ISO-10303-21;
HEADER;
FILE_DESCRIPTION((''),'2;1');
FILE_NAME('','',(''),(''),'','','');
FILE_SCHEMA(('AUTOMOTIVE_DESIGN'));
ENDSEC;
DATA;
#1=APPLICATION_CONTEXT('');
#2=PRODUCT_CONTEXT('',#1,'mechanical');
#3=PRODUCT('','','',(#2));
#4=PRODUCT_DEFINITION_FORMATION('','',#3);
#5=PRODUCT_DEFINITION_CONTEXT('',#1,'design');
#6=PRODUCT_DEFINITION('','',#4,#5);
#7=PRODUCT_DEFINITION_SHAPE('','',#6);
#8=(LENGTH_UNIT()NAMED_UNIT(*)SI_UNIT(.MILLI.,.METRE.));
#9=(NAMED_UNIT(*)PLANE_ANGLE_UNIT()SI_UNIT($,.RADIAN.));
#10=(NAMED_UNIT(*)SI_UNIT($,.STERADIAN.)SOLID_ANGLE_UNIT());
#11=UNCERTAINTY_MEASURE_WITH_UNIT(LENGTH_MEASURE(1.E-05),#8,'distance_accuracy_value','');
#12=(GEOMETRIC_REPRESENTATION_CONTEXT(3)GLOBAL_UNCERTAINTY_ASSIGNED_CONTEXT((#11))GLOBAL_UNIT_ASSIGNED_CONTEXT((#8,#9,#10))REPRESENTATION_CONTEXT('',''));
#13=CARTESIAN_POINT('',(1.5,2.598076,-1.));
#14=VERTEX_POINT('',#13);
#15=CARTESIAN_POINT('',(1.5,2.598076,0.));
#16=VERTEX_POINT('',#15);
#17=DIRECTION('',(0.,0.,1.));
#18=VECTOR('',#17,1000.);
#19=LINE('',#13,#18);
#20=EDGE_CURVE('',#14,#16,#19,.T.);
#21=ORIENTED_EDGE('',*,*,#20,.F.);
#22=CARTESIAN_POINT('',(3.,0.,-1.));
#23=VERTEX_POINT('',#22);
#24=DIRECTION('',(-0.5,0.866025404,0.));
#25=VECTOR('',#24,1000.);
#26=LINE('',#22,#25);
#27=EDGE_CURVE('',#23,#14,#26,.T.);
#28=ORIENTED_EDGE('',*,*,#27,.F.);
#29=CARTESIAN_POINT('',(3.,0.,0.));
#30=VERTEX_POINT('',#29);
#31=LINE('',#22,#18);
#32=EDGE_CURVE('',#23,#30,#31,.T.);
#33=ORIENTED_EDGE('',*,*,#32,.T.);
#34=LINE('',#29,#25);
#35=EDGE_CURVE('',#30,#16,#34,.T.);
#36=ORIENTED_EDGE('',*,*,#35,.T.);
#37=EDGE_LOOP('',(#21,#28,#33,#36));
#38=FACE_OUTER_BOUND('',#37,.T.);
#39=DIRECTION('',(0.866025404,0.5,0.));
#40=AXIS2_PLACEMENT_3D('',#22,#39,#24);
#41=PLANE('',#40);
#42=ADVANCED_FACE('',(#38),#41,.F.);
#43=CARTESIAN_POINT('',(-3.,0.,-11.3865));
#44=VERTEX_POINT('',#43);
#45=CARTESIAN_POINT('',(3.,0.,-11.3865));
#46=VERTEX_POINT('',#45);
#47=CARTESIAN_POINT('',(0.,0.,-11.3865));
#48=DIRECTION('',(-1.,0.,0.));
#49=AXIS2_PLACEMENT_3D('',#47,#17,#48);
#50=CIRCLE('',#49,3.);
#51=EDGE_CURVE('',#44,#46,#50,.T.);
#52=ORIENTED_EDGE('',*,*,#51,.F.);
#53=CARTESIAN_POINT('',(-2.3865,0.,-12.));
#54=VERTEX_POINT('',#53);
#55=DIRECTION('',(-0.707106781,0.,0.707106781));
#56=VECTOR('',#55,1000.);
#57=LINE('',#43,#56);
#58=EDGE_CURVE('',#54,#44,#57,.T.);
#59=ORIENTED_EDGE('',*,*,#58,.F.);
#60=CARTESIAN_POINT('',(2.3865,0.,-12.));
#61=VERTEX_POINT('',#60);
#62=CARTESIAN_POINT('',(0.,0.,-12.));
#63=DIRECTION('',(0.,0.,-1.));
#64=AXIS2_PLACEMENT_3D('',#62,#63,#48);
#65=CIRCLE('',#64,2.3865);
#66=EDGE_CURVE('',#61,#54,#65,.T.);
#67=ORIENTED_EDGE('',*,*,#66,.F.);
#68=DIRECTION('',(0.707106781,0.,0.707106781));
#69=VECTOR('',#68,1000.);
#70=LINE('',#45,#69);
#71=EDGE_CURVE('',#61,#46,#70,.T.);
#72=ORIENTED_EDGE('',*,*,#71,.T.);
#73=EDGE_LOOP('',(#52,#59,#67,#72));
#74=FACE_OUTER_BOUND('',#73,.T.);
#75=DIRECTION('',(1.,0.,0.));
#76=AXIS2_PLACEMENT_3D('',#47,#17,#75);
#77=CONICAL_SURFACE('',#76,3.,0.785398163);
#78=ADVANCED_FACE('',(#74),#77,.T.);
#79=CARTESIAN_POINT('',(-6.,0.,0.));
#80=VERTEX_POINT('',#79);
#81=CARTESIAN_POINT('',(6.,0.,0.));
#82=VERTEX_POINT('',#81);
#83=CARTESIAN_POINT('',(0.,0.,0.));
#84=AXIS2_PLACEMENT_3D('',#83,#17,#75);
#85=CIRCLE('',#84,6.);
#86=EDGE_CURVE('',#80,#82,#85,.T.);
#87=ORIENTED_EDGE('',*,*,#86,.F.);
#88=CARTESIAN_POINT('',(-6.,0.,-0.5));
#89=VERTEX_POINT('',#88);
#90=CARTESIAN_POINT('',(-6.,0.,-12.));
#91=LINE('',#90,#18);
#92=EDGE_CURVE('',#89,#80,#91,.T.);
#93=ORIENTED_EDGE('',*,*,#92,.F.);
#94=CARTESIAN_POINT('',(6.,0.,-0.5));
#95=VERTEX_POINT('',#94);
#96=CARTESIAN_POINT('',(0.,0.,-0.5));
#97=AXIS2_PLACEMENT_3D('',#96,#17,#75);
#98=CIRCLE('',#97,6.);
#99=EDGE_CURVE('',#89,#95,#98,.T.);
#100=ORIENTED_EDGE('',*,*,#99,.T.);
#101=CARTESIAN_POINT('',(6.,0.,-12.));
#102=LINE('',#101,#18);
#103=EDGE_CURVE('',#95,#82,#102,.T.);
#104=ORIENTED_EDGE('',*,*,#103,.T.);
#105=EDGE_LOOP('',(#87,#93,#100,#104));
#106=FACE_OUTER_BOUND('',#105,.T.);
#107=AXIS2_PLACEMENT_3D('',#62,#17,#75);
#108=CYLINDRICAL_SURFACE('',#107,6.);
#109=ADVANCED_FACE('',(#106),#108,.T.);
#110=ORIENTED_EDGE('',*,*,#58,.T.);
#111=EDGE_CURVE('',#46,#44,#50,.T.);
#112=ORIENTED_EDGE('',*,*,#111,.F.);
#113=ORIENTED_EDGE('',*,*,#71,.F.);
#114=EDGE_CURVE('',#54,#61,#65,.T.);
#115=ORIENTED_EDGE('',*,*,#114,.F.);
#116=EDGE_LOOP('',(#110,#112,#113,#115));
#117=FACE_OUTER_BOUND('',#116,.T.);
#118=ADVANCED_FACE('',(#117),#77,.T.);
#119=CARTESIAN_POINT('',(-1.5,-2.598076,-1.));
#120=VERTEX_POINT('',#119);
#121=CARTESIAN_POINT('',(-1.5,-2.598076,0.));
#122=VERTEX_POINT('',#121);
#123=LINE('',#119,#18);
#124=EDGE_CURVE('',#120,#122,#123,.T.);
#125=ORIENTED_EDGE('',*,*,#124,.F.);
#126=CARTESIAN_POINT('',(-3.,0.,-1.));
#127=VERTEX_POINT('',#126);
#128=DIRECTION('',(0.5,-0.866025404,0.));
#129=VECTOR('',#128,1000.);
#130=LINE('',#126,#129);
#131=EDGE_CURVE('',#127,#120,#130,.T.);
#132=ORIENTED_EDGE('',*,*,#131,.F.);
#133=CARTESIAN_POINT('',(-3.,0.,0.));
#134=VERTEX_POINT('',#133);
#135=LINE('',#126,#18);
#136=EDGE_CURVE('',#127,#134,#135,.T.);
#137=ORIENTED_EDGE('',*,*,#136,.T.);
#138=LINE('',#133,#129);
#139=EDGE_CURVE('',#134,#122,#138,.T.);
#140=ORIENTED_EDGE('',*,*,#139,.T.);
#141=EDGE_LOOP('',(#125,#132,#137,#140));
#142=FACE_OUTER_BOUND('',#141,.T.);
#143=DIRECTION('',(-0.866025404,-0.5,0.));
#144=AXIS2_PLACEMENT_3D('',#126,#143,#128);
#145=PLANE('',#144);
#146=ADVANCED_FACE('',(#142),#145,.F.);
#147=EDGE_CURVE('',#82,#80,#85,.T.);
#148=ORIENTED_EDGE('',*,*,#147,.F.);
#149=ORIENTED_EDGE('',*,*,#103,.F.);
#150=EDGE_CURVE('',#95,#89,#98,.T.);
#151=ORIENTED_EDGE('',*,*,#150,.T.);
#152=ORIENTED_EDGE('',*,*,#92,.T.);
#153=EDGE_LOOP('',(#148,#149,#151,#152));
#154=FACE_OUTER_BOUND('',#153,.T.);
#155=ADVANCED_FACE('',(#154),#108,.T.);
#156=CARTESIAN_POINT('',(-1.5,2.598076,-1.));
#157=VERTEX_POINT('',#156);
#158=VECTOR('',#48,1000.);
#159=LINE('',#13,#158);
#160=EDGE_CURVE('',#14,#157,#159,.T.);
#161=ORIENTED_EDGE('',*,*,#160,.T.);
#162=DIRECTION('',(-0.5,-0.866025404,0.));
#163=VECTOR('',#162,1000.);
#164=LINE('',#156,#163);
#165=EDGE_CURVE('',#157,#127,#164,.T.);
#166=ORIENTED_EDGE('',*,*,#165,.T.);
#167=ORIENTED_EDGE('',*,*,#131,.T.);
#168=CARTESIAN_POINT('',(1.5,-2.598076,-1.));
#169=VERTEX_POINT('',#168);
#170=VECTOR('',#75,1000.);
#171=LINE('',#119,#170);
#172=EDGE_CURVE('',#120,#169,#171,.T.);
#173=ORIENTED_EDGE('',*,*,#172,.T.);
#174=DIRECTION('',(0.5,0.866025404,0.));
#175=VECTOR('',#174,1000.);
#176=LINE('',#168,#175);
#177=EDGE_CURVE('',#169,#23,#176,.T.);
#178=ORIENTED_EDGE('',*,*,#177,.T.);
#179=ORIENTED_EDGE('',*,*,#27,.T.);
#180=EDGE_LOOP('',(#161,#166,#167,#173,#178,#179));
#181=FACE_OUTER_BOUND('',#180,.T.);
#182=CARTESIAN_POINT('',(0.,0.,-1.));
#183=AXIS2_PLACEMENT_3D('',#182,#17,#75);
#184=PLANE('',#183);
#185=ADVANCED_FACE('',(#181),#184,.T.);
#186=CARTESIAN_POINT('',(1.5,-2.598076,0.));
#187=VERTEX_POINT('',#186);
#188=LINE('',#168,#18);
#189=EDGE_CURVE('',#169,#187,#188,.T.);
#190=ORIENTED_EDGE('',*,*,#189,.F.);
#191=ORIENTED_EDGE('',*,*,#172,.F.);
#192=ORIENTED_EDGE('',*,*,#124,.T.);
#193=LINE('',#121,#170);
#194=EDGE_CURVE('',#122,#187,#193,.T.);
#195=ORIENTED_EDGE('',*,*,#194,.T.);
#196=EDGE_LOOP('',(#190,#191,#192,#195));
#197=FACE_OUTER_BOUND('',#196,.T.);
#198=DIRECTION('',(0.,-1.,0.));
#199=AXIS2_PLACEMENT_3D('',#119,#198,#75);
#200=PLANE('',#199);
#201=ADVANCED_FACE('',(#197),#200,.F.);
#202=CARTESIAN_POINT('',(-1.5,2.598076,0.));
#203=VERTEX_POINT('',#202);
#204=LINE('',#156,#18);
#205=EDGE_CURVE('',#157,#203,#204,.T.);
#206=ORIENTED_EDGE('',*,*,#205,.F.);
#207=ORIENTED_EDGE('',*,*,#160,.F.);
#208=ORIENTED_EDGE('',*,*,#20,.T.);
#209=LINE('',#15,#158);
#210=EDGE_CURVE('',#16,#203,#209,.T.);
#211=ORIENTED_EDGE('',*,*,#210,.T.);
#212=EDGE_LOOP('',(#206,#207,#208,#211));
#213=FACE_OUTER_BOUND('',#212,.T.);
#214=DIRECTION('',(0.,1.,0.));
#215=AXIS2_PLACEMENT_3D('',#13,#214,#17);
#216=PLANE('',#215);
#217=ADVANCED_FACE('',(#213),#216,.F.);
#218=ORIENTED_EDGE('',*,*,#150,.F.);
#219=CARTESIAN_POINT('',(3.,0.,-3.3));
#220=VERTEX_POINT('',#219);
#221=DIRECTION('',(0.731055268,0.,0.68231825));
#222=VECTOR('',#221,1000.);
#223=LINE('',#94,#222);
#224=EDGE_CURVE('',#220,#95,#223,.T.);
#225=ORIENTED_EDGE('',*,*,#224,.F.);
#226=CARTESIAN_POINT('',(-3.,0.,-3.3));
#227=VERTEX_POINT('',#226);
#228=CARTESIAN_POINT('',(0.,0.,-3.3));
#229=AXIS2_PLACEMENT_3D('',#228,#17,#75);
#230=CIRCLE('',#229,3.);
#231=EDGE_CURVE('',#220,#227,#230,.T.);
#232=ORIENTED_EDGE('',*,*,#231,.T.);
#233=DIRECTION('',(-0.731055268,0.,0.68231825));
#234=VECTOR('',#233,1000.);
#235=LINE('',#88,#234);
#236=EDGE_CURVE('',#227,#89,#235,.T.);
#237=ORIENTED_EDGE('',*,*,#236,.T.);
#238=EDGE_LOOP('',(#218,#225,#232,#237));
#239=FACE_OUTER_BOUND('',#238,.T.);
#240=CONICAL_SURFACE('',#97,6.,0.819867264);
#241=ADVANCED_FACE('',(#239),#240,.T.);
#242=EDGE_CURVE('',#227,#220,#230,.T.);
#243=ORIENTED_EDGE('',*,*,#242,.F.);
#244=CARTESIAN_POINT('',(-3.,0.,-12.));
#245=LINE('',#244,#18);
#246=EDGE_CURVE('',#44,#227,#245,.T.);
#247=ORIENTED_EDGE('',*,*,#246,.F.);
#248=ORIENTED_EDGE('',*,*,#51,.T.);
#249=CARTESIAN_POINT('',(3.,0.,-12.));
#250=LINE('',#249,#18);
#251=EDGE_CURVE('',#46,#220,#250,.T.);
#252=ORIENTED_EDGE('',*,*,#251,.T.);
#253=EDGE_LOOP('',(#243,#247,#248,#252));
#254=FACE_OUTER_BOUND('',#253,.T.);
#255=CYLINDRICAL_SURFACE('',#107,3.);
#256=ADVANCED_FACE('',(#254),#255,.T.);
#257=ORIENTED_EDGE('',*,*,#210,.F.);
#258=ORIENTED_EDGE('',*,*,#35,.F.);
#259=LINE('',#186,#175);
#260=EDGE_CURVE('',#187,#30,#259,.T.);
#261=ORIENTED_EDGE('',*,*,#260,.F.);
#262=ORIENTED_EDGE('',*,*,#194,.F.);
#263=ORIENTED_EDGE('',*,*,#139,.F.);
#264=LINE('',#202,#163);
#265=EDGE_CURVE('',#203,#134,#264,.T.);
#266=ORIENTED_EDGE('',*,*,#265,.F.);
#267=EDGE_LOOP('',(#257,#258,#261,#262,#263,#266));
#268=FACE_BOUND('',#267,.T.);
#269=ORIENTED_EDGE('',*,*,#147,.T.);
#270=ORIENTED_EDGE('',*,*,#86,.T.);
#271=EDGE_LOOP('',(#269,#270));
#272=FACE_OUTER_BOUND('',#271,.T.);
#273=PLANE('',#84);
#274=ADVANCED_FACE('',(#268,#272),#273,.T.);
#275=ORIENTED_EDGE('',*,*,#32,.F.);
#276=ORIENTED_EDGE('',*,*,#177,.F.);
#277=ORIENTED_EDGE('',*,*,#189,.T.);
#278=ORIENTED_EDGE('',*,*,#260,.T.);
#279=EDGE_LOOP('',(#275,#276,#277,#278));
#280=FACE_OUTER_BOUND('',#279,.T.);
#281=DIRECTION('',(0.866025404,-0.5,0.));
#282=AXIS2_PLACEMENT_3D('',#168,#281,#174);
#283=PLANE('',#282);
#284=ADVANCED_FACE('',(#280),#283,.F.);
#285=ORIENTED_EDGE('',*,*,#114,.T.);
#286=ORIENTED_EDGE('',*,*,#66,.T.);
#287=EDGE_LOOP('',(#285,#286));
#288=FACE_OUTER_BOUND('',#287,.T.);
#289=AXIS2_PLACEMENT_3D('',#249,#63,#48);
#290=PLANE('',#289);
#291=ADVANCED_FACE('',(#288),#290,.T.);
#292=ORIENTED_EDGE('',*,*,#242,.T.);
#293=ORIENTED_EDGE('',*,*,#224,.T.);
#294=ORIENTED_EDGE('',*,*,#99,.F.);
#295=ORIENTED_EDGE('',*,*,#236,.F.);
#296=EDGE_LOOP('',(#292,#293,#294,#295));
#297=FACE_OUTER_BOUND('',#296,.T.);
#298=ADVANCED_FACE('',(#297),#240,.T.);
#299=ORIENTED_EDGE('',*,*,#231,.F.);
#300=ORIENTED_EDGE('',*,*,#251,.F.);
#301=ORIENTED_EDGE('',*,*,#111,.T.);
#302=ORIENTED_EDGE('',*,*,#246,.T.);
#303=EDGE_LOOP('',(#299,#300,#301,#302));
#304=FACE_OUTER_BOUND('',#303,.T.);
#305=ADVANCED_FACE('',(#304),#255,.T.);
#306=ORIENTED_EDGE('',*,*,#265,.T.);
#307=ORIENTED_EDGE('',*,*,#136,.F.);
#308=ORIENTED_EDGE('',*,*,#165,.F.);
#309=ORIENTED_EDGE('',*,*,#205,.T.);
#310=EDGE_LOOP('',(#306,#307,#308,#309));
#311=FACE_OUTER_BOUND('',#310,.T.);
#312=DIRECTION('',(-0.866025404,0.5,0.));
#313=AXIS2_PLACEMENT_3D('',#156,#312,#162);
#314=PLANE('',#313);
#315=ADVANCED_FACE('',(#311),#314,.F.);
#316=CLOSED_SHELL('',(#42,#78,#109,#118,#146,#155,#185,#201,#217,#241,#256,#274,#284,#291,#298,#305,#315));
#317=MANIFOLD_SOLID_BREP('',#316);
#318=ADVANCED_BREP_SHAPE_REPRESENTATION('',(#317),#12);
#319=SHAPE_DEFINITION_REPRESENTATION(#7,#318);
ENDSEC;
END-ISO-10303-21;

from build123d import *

# Parameters (mm, degrees)
CUT_EXTRUDE_1_DEPTH = 1
CHAMFER_1_SIZE      = 0.6135


with BuildPart() as part:
    # 草图1 → 旋转1 (revolve)
    with BuildSketch(Plane(origin=(0, 0, 0), x_dir=(1, 0, 0), z_dir=(0, 1, 0))):
        Polygon((3, 12), (0, 12), (0, 0), (6, 0), (6, 0.5), (3, 3.3), align=None)
    revolve(axis=Axis((0, 0, -12), (0, 0, 1)))

    # 草图2 → 切除-拉伸1 (cut)
    with BuildSketch(Plane.XY):
        Polygon((1.5, -2.598076211), (3, 0), (1.5, 2.598076211), (-1.5, 2.598076211), (-3, 0), (-1.5, -2.598076211), align=None)
    extrude(amount=-CUT_EXTRUDE_1_DEPTH, mode=Mode.SUBTRACT)

    # 倒角1
    chamfer_1_edges = [part.edges().sort_by_distance(p)[0] for p in [
        (-3, 0, -12),
    ]]
    chamfer(chamfer_1_edges, length=CHAMFER_1_SIZE)


solid = part.part
